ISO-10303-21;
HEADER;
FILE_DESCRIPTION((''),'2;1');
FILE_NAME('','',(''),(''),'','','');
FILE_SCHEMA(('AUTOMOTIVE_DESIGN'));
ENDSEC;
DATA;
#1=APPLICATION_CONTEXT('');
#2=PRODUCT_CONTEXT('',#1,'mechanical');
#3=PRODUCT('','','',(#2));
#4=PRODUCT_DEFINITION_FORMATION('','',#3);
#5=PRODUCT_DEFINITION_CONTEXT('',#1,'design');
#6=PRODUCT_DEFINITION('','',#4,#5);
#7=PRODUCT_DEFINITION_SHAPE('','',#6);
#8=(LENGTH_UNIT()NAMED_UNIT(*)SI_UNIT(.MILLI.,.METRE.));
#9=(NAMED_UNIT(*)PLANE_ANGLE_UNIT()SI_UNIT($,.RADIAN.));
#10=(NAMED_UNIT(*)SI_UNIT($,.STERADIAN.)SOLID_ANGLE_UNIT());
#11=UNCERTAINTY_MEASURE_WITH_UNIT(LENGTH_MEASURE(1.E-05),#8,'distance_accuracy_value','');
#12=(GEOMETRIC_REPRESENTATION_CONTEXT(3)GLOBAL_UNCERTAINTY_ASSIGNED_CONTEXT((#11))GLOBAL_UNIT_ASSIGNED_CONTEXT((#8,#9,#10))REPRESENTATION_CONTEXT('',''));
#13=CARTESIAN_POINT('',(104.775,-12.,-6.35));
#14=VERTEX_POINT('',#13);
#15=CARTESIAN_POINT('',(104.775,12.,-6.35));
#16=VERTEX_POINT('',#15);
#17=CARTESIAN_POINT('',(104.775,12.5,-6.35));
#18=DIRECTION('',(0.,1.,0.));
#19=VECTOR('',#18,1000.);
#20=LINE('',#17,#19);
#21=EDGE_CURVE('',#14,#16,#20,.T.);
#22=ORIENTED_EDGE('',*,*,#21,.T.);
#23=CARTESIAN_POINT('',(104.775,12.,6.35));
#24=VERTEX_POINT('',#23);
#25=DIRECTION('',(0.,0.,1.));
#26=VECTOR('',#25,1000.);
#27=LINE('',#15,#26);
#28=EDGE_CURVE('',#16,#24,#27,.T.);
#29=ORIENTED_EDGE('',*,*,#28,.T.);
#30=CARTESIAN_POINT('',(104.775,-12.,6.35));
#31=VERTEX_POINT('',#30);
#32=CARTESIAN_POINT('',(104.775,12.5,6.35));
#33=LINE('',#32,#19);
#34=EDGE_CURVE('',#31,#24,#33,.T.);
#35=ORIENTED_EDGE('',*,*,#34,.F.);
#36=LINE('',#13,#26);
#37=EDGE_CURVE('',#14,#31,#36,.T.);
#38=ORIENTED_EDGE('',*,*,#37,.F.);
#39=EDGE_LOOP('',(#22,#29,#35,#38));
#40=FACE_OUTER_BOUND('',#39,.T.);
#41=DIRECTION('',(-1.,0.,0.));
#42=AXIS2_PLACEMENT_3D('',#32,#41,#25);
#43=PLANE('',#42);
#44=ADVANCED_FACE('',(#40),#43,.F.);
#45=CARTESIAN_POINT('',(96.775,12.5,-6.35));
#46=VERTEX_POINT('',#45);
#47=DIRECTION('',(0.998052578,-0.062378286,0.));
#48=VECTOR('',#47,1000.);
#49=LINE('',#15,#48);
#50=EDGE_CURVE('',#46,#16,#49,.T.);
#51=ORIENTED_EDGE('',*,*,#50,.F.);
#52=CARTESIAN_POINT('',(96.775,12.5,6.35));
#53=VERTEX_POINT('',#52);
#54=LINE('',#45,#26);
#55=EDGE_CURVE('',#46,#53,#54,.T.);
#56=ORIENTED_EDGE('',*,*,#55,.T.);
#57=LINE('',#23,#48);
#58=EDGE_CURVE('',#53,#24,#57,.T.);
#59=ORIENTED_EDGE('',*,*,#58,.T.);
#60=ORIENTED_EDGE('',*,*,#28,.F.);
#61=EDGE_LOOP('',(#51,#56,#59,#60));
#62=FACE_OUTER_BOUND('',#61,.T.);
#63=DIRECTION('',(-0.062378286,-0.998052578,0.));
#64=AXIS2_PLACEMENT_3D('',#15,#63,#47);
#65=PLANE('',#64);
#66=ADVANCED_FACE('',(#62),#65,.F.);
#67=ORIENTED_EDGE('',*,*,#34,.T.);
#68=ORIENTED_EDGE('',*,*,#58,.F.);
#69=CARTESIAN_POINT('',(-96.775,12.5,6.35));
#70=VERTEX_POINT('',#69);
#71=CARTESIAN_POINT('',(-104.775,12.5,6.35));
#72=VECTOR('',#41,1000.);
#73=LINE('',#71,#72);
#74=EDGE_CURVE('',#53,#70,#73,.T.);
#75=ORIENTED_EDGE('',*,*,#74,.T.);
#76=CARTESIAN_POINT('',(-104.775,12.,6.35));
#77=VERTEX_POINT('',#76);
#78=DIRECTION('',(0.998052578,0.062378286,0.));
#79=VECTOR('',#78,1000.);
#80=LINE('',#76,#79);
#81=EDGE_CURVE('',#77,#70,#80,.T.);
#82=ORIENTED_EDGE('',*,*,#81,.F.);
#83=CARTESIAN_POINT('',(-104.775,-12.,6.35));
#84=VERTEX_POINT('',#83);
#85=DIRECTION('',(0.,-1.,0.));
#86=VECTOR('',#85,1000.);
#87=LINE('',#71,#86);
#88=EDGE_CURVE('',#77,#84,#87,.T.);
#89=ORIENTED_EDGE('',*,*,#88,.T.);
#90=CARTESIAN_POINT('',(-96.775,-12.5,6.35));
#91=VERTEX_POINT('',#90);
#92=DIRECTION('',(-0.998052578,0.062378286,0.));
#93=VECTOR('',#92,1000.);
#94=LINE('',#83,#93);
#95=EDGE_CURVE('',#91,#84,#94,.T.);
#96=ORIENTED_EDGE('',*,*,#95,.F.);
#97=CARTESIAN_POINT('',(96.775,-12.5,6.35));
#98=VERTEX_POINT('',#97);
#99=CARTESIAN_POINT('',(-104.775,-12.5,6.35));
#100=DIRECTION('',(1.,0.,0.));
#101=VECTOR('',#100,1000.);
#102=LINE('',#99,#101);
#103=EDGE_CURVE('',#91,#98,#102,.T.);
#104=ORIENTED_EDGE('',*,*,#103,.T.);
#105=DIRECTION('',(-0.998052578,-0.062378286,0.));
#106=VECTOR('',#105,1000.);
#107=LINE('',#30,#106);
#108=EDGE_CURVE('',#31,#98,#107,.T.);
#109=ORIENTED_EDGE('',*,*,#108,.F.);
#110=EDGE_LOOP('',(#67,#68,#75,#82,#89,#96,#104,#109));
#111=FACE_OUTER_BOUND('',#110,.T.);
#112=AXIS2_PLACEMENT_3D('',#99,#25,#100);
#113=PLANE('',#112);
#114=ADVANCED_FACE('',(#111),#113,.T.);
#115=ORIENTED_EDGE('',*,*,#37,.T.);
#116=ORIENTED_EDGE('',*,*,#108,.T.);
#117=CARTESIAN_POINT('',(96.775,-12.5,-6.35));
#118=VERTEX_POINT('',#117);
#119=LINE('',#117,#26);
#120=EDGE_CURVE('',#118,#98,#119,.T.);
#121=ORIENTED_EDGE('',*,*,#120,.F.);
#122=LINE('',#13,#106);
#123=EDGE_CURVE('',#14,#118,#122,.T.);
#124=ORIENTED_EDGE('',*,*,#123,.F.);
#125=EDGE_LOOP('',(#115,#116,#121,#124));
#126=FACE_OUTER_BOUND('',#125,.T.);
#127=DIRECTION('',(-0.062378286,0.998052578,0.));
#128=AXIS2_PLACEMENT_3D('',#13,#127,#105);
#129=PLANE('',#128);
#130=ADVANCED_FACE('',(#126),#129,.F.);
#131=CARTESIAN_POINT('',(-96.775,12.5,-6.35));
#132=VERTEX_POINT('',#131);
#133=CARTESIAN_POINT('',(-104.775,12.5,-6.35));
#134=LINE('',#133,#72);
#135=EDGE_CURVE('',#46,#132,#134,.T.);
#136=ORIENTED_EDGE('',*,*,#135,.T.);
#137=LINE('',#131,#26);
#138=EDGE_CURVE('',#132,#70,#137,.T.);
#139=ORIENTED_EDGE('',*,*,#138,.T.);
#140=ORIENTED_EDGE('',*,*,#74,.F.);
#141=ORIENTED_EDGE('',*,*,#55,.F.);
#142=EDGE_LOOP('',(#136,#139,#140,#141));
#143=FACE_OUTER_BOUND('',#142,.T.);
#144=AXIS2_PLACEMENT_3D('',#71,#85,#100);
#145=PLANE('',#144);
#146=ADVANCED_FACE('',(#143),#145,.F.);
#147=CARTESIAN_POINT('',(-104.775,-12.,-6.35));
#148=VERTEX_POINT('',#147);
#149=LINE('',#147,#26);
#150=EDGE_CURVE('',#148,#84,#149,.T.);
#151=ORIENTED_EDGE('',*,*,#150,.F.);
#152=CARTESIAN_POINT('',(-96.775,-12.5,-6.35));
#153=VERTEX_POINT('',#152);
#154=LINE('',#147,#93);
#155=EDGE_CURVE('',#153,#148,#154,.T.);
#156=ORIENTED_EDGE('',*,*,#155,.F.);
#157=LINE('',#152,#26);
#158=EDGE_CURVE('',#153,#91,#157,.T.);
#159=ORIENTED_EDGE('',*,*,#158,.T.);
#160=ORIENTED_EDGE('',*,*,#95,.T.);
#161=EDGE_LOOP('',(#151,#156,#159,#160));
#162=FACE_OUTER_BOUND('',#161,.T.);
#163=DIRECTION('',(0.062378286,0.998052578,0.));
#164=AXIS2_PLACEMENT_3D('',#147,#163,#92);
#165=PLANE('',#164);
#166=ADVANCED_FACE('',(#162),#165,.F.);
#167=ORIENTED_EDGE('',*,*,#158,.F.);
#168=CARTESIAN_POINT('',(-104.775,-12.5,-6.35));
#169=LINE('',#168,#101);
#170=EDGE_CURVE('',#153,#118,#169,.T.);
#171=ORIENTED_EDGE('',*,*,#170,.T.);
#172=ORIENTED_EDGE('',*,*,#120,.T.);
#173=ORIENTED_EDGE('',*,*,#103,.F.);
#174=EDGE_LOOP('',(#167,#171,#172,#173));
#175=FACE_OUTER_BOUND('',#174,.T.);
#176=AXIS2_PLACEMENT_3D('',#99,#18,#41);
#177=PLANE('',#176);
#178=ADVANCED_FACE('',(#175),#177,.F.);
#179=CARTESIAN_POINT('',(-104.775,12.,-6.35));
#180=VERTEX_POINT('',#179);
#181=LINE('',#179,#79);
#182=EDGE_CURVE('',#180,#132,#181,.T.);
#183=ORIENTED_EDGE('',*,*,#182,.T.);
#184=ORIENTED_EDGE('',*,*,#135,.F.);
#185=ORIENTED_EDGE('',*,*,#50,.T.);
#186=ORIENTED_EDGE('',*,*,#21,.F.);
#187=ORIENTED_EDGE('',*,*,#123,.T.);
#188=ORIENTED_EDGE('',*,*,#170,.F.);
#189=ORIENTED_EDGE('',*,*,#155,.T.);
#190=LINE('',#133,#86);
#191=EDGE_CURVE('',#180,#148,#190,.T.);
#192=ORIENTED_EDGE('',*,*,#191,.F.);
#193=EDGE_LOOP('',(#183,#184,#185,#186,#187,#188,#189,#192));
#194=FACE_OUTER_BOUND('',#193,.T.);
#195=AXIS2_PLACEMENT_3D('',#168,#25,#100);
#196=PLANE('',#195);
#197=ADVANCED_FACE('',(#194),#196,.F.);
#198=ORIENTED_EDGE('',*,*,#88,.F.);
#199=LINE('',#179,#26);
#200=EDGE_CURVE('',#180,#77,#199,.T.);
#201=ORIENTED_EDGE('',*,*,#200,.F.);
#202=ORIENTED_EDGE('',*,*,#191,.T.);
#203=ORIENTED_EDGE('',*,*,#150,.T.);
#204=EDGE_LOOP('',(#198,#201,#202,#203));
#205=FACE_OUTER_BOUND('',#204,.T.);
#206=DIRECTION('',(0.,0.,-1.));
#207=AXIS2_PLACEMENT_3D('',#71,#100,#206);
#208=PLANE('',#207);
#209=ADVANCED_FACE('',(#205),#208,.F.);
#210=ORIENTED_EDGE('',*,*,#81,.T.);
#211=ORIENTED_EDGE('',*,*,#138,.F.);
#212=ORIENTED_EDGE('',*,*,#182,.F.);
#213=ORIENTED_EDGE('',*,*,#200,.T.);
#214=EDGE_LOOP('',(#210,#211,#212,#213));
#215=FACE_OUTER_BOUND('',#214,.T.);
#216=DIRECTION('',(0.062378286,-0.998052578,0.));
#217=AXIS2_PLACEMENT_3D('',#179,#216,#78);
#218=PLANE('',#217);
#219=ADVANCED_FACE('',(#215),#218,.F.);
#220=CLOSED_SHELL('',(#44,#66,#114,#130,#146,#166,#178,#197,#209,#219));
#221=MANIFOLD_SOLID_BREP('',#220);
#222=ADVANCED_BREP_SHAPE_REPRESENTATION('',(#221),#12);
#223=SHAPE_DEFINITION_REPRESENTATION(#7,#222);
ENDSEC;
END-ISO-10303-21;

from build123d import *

# Parameters (mm, degrees)
SKETCH1_W          = 209.55
SKETCH1_H          = 25
EXTRUDE1_DEPTH     = 6.35
CUT_EXTRUDE1_DEPTH = 107.279540011


with BuildPart() as part:
    # Sketch1 → Extrude1 (new, symmetric)
    with BuildSketch(Plane.XY):
        Rectangle(SKETCH1_W, SKETCH1_H)
    extrude(amount=EXTRUDE1_DEPTH, both=True)

    # Sketch2 → Cut-Extrude1 (cut, through all)
    with BuildSketch(Plane.XY.offset(6.35)):
        Polygon((-104.775, 12), (-96.775, 12.5), (-104.775, 12.5), align=None)
        Polygon((96.775, 12.5), (104.775, 12.5), (104.775, 12), align=None)
        Polygon((104.775, -12.5), (104.775, -12), (96.775, -12.5), align=None)
        Polygon((-96.775, -12.5), (-104.775, -12.5), (-104.775, -12), align=None)
    extrude(amount=-CUT_EXTRUDE1_DEPTH, mode=Mode.SUBTRACT)


solid = part.part
